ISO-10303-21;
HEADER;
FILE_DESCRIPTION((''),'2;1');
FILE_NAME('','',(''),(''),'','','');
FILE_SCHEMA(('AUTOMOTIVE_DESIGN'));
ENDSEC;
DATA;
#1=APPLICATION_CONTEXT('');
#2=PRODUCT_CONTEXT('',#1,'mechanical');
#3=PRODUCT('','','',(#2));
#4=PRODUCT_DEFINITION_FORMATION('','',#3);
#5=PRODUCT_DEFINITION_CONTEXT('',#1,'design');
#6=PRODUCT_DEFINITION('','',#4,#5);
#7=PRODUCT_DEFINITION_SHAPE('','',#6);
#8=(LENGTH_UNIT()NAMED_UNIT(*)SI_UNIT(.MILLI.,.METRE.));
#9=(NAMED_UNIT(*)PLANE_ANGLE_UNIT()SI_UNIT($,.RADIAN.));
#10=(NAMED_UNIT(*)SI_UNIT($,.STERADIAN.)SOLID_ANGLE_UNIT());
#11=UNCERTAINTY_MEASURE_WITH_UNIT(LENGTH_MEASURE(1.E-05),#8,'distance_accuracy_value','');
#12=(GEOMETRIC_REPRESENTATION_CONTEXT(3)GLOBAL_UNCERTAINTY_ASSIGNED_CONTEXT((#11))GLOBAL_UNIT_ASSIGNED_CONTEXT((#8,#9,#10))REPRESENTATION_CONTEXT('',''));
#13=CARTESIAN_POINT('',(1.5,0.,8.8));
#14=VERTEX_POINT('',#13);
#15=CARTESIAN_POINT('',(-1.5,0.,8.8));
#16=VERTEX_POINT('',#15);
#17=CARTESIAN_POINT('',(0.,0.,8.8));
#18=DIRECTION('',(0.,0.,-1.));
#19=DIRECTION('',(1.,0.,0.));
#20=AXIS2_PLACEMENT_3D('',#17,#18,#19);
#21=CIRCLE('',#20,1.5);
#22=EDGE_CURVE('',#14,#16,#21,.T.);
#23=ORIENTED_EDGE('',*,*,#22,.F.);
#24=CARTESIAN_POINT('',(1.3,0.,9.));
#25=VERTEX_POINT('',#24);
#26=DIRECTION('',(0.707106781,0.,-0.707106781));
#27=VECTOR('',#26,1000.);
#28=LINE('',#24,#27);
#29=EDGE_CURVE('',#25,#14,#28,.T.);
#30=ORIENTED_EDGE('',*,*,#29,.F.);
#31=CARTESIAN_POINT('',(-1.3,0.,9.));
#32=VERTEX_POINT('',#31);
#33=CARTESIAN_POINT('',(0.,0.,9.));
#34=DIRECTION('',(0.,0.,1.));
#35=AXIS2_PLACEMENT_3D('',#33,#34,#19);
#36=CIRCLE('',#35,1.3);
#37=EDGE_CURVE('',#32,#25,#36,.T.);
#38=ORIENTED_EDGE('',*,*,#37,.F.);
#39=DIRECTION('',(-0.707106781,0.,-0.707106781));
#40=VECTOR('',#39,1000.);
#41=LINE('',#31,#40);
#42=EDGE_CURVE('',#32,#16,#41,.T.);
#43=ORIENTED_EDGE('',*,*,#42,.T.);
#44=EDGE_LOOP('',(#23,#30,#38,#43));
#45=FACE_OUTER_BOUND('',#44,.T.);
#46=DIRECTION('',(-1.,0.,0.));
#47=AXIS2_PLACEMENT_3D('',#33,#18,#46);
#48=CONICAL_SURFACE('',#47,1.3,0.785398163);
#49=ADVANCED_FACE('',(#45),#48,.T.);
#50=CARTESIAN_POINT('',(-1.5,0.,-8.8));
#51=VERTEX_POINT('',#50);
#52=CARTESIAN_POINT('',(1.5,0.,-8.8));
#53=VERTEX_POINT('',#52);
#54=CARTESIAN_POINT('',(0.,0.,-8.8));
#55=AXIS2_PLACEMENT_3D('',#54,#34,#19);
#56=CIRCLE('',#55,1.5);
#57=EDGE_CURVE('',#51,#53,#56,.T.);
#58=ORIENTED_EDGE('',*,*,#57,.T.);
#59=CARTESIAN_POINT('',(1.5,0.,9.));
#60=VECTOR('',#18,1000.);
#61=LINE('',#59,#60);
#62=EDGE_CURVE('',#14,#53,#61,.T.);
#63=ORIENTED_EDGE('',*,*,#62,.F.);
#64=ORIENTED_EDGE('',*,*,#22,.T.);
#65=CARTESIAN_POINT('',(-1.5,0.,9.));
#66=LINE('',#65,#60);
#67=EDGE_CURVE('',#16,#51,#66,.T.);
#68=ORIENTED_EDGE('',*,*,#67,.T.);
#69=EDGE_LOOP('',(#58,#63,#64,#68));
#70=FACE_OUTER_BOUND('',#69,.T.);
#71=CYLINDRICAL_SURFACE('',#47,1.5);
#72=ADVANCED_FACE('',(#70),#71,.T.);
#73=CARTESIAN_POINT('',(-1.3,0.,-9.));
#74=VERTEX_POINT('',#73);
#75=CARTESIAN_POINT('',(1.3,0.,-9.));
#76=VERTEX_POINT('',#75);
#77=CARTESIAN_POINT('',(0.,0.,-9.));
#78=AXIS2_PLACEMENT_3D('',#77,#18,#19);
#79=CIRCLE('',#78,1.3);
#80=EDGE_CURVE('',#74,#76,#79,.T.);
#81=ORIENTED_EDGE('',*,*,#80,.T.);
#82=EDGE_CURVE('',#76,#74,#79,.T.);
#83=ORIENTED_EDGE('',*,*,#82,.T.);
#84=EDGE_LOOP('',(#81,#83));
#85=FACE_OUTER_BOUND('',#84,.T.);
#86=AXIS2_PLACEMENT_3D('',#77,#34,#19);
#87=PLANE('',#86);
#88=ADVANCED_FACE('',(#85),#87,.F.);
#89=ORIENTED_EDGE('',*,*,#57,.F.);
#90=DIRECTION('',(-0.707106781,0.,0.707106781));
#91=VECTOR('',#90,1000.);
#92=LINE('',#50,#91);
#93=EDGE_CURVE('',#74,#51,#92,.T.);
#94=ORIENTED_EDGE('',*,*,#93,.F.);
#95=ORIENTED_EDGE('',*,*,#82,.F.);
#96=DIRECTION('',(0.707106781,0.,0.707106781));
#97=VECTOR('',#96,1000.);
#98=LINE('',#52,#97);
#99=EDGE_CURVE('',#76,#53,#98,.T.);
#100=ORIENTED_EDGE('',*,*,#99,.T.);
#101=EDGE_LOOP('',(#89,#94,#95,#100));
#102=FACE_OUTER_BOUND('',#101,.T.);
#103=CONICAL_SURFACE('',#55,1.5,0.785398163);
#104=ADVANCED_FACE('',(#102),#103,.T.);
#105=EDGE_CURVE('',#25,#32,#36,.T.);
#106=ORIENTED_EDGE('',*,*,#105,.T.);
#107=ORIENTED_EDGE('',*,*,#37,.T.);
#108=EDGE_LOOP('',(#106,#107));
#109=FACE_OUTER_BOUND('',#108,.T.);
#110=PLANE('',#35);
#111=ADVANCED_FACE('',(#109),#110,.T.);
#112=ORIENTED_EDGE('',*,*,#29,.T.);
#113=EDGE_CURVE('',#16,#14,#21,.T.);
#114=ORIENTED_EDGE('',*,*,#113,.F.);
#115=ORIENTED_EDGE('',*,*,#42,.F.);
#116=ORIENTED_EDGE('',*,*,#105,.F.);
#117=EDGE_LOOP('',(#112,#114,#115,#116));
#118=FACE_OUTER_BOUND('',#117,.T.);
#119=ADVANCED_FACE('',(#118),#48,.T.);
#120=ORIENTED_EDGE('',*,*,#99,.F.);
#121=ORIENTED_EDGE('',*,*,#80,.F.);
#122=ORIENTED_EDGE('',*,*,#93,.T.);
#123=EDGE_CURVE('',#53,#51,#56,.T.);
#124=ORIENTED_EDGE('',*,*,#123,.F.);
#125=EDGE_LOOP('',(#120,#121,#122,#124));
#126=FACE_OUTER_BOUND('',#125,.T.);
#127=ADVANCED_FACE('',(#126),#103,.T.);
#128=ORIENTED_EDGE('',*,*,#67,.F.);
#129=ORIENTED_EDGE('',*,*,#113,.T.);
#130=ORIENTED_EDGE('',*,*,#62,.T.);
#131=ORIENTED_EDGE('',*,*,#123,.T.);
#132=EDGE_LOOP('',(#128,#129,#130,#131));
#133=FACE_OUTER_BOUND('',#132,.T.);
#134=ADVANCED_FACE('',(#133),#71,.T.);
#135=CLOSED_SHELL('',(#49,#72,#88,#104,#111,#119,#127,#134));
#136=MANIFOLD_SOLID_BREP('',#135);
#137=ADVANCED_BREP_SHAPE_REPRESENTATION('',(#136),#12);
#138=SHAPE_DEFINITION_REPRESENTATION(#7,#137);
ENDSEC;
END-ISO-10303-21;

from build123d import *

# Parameters (mm, degrees)
PIN_PROFILE_3_R          = 1.5
PIN_BODY_3X18_DEPTH      = 9
END_CHAMFERS_0_2X45_SIZE = 0.2


with BuildPart() as part:
    # Pin Profile Ø3 → Pin Body Ø3x18 (new, symmetric)
    with BuildSketch(Plane.XY):
        Circle(PIN_PROFILE_3_R)
    extrude(amount=PIN_BODY_3X18_DEPTH, both=True)

    # End Chamfers 0.2x45°
    end_chamfers_0_2x45_edges = [part.edges().sort_by_distance(p)[0] for p in [
        (-1.5, 0, -9),
        (-1.5, 0, 9),
    ]]
    chamfer(end_chamfers_0_2x45_edges, length=END_CHAMFERS_0_2X45_SIZE)


solid = part.part
